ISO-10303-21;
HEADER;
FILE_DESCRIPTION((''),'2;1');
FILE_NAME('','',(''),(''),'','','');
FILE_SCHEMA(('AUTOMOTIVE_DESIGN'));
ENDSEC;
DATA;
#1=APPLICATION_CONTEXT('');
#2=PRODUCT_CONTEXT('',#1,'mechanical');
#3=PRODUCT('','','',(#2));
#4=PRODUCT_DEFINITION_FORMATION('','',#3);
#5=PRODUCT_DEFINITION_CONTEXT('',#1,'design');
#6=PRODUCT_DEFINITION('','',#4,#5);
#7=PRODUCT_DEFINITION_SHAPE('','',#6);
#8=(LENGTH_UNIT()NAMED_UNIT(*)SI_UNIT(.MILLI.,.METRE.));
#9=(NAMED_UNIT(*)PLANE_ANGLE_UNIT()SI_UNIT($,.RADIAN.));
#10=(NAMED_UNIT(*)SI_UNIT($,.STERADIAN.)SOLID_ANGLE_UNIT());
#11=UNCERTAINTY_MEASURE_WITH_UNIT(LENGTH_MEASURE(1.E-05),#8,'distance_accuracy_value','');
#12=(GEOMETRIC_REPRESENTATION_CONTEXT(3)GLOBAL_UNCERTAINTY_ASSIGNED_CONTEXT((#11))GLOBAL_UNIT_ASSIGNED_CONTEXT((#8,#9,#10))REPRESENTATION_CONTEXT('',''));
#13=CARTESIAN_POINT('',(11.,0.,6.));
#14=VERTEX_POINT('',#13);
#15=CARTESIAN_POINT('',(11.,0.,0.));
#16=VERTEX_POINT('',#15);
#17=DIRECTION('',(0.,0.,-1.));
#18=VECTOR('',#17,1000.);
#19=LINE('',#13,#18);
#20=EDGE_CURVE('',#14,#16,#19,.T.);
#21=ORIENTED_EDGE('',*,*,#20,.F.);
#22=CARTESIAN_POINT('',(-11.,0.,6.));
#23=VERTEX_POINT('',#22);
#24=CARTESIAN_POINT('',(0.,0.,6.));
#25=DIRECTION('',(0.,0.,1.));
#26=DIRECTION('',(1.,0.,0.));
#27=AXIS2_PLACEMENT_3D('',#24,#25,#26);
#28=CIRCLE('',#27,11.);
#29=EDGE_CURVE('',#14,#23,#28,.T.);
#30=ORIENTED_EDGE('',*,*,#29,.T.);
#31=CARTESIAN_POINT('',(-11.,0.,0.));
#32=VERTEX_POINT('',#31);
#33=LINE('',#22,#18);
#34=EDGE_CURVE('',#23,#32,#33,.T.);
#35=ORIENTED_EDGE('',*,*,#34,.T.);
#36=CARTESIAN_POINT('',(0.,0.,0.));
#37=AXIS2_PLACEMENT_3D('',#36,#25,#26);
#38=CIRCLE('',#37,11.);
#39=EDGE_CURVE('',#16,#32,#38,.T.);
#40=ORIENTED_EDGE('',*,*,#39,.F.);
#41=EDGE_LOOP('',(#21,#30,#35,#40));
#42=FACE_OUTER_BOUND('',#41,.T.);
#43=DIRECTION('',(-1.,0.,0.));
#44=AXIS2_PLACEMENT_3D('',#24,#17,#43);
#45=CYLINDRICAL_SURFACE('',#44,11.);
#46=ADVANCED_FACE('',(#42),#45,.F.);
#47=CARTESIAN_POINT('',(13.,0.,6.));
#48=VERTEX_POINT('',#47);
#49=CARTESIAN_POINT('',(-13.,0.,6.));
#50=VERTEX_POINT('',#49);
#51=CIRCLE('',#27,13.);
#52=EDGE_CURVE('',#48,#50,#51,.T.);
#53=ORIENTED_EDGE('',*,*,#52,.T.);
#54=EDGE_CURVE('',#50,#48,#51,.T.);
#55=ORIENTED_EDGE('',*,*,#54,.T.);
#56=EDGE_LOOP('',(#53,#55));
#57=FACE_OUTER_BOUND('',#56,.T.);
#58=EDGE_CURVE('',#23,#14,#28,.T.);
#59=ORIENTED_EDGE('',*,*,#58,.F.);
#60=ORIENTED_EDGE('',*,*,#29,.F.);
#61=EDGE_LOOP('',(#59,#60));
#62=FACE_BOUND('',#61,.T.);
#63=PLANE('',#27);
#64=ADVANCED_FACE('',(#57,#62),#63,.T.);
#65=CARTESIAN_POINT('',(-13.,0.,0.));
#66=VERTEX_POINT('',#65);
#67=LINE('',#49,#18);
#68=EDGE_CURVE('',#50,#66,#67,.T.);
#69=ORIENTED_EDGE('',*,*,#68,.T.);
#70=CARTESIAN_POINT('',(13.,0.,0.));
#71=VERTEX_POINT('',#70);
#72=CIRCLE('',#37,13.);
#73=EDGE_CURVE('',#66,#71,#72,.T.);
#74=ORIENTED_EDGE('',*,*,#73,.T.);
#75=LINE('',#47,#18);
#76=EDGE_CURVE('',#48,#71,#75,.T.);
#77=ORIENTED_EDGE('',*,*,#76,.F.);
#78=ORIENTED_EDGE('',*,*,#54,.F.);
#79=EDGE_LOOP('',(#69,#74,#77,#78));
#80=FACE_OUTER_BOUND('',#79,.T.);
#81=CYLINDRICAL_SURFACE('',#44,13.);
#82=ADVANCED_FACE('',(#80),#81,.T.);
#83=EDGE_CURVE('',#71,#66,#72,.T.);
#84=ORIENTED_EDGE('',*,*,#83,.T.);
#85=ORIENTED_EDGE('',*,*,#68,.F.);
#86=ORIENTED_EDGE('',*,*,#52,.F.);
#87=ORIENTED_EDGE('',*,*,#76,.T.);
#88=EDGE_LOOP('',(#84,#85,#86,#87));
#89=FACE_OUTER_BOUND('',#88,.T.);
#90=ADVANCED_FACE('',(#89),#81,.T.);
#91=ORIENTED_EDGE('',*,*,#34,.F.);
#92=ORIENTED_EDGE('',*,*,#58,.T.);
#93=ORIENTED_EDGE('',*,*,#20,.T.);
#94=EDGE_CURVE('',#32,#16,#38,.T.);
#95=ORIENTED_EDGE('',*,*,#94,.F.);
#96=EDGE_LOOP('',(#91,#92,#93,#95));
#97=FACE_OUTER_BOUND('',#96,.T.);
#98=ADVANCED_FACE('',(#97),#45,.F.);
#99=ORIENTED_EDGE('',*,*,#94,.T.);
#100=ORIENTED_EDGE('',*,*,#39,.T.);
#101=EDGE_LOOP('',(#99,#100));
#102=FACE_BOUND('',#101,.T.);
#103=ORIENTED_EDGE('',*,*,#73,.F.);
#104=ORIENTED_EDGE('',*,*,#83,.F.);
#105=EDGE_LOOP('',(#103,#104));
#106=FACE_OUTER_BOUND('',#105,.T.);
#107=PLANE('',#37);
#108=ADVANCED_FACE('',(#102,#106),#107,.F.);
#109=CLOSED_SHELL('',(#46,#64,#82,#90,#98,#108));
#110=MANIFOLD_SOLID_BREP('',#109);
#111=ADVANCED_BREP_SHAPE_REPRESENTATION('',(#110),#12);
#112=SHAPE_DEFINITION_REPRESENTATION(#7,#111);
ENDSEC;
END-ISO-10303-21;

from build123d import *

# Parameters (mm, degrees)
SKETCH1_R           = 13
SKETCH1_R_2         = 11
BOSS_EXTRUDE1_DEPTH = 6


with BuildPart() as part:
    # Sketch1 → Boss-Extrude1 (new body)
    with BuildSketch(Plane.XY):
        Circle(SKETCH1_R)
        Circle(SKETCH1_R_2, mode=Mode.SUBTRACT)
    extrude(amount=BOSS_EXTRUDE1_DEPTH)


solid = part.part
